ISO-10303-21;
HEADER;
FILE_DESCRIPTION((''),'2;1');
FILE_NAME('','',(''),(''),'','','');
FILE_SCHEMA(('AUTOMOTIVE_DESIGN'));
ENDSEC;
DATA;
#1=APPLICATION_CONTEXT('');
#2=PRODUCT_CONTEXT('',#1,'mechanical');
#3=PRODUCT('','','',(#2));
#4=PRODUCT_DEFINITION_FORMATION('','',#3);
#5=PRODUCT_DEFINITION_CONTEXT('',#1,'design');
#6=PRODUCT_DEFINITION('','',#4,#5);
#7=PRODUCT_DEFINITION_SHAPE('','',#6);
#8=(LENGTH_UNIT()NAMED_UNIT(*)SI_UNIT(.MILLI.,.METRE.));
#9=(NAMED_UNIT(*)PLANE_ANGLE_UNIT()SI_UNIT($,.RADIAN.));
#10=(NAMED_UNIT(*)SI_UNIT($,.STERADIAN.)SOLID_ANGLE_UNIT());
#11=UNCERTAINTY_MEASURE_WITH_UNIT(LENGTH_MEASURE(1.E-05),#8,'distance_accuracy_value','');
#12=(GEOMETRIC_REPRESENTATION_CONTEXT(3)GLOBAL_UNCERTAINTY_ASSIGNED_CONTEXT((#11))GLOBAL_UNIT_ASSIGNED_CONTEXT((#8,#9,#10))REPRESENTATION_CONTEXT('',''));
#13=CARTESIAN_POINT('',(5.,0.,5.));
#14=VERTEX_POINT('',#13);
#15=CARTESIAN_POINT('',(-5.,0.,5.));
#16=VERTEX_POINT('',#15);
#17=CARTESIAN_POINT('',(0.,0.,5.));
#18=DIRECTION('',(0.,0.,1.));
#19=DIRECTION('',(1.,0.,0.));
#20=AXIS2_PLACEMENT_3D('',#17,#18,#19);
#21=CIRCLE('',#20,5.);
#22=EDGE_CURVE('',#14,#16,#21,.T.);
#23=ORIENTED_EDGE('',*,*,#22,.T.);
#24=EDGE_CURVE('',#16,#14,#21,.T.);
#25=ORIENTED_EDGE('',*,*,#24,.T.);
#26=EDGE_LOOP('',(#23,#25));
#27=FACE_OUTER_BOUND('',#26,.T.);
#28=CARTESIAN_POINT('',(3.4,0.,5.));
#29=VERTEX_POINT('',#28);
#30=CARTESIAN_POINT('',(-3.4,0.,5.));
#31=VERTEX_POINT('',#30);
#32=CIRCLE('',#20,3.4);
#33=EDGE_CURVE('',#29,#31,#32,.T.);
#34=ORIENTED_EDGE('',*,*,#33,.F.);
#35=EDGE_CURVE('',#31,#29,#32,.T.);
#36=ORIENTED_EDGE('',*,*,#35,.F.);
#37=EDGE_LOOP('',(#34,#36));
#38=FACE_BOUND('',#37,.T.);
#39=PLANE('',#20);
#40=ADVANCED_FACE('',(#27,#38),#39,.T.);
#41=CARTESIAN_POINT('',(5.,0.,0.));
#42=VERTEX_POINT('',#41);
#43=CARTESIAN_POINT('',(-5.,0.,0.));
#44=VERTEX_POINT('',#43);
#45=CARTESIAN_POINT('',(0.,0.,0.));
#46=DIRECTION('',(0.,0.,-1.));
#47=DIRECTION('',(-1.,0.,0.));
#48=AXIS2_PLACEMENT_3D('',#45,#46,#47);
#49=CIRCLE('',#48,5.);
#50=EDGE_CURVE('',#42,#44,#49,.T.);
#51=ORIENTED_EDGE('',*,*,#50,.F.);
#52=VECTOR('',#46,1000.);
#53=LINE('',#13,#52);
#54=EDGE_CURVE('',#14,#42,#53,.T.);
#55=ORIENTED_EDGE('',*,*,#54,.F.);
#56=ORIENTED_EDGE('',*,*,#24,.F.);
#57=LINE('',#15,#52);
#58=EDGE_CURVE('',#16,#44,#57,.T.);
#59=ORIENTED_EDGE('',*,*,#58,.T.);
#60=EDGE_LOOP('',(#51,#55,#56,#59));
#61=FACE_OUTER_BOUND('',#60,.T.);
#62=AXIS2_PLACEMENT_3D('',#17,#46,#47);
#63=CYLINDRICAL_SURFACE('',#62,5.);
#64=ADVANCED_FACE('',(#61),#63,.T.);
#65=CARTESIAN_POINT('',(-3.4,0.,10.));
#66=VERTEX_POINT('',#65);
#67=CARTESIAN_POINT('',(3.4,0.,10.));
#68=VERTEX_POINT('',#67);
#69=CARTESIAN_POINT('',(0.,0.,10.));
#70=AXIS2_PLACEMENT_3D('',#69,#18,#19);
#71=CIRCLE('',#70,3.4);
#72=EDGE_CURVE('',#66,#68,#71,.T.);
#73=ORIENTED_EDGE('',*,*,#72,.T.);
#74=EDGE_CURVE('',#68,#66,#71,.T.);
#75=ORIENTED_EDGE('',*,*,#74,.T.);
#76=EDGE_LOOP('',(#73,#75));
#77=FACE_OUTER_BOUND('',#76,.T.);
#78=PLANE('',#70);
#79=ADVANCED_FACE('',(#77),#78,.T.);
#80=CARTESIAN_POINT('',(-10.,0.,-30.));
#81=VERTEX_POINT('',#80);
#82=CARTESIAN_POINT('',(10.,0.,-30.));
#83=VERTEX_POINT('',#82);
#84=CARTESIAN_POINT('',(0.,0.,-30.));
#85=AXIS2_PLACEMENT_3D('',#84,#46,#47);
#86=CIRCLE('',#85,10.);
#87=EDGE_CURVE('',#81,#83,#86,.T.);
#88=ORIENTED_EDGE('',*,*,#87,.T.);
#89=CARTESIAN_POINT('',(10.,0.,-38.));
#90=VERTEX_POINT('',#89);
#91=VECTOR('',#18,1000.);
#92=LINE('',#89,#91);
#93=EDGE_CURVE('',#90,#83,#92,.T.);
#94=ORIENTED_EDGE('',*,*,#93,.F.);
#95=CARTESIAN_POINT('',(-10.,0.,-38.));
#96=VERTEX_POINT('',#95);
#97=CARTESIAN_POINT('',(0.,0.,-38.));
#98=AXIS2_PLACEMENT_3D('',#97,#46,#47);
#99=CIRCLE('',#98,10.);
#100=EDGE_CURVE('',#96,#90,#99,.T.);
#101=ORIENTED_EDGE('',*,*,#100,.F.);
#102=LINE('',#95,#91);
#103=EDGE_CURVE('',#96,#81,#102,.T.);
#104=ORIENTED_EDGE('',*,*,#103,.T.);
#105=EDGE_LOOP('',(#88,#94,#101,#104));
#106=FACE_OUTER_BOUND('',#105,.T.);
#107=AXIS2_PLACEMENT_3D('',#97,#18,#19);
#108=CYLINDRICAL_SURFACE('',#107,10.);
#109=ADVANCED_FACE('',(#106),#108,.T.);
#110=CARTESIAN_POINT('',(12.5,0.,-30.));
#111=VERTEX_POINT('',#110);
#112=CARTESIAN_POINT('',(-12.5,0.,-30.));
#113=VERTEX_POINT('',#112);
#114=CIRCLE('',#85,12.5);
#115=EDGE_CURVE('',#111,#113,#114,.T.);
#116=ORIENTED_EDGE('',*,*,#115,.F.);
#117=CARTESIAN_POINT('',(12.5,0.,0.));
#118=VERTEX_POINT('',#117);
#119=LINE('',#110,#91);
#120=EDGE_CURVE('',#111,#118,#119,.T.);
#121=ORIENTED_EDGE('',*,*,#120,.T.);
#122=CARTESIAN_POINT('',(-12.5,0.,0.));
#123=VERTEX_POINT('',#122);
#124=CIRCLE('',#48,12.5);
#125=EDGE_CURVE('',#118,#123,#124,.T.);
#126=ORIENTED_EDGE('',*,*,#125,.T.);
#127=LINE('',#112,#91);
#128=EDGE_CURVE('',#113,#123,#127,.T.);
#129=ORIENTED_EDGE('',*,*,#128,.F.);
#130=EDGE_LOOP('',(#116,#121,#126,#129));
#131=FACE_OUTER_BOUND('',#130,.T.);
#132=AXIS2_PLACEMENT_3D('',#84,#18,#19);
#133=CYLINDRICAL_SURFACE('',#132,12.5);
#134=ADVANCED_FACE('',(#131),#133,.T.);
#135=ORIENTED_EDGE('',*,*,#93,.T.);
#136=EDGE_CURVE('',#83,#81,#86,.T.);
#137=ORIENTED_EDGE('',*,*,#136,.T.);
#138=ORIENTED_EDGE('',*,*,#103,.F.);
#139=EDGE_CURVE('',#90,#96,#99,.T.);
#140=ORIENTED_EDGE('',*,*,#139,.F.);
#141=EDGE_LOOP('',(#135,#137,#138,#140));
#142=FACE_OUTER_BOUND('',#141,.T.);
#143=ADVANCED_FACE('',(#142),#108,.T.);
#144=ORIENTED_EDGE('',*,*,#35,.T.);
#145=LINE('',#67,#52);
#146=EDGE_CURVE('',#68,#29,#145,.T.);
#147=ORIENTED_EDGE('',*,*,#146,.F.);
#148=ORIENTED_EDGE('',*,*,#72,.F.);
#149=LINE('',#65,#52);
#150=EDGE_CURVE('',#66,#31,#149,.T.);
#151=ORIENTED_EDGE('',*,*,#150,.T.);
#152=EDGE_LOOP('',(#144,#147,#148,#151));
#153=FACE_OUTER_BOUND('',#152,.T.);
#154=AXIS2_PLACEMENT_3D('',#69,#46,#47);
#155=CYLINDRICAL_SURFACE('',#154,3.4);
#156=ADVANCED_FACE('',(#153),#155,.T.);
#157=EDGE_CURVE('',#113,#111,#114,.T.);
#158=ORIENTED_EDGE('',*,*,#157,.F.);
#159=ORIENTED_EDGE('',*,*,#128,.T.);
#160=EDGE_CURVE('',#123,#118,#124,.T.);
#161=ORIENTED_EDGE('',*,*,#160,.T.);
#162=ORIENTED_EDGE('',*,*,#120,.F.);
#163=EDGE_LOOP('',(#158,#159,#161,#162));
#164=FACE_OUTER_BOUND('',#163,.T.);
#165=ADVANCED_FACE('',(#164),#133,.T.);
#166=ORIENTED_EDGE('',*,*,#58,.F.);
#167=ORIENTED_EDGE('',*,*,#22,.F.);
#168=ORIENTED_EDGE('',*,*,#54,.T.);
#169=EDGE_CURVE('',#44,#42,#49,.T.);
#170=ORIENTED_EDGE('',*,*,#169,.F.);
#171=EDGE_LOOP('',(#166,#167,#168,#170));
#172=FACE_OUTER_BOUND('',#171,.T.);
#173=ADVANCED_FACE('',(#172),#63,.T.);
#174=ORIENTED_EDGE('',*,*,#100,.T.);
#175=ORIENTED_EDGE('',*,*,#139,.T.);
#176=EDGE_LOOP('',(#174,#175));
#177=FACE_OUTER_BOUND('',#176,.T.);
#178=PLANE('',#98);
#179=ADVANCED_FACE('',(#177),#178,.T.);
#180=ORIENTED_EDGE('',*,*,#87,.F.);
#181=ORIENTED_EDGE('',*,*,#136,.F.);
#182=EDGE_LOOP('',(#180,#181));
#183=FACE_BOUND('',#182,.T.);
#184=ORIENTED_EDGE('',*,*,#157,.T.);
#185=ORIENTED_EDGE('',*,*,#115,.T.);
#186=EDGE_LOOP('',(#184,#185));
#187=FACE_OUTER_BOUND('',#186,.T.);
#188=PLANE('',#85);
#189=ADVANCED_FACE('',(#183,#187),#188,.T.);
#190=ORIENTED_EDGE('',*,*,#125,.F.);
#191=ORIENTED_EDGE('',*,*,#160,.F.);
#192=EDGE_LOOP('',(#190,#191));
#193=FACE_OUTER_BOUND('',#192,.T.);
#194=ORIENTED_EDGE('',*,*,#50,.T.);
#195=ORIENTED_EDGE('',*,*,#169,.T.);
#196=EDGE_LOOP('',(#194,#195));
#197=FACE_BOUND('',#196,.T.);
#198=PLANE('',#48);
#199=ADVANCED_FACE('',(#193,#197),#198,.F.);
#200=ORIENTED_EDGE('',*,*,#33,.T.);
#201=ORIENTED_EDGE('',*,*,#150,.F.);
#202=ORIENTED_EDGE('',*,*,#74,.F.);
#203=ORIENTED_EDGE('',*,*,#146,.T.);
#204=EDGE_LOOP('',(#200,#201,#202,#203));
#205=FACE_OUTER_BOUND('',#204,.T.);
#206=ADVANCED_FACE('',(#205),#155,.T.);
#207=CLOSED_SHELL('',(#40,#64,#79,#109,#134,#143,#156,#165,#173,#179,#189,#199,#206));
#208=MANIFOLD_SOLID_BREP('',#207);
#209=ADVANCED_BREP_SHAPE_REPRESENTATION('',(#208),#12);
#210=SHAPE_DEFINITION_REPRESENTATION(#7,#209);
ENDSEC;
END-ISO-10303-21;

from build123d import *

# Parameters (mm, degrees)
SKETCH1_R           = 5
BOSS_EXTRUDE1_DEPTH = 5
SKETCH2_R           = 3.4
BOSS_EXTRUDE2_DEPTH = 5
SKETCH3_R           = 12.5
BOSS_EXTRUDE3_DEPTH = 30
SKETCH4_R           = 10
BOSS_EXTRUDE4_DEPTH = 8


with BuildPart() as part:
    # Sketch1 → Boss-Extrude1 (new body)
    with BuildSketch(Plane.XY):
        Circle(SKETCH1_R)
    extrude(amount=BOSS_EXTRUDE1_DEPTH)

    # Sketch2 → Boss-Extrude2 (add)
    with BuildSketch(Plane.XY.offset(5)):
        Circle(SKETCH2_R)
    extrude(amount=BOSS_EXTRUDE2_DEPTH)

    # Sketch3 → Boss-Extrude3 (add)
    with BuildSketch(Plane(origin=(0, 0, 0), x_dir=(-1, 0, 0), z_dir=(0, 0, -1))):
        Circle(SKETCH3_R)
    extrude(amount=BOSS_EXTRUDE3_DEPTH)

    # Sketch4 → Boss-Extrude4 (add)
    with BuildSketch(Plane(origin=(0, 0, -30), x_dir=(-1, 0, 0), z_dir=(0, 0, -1))):
        Circle(SKETCH4_R)
    extrude(amount=BOSS_EXTRUDE4_DEPTH)


solid = part.part
